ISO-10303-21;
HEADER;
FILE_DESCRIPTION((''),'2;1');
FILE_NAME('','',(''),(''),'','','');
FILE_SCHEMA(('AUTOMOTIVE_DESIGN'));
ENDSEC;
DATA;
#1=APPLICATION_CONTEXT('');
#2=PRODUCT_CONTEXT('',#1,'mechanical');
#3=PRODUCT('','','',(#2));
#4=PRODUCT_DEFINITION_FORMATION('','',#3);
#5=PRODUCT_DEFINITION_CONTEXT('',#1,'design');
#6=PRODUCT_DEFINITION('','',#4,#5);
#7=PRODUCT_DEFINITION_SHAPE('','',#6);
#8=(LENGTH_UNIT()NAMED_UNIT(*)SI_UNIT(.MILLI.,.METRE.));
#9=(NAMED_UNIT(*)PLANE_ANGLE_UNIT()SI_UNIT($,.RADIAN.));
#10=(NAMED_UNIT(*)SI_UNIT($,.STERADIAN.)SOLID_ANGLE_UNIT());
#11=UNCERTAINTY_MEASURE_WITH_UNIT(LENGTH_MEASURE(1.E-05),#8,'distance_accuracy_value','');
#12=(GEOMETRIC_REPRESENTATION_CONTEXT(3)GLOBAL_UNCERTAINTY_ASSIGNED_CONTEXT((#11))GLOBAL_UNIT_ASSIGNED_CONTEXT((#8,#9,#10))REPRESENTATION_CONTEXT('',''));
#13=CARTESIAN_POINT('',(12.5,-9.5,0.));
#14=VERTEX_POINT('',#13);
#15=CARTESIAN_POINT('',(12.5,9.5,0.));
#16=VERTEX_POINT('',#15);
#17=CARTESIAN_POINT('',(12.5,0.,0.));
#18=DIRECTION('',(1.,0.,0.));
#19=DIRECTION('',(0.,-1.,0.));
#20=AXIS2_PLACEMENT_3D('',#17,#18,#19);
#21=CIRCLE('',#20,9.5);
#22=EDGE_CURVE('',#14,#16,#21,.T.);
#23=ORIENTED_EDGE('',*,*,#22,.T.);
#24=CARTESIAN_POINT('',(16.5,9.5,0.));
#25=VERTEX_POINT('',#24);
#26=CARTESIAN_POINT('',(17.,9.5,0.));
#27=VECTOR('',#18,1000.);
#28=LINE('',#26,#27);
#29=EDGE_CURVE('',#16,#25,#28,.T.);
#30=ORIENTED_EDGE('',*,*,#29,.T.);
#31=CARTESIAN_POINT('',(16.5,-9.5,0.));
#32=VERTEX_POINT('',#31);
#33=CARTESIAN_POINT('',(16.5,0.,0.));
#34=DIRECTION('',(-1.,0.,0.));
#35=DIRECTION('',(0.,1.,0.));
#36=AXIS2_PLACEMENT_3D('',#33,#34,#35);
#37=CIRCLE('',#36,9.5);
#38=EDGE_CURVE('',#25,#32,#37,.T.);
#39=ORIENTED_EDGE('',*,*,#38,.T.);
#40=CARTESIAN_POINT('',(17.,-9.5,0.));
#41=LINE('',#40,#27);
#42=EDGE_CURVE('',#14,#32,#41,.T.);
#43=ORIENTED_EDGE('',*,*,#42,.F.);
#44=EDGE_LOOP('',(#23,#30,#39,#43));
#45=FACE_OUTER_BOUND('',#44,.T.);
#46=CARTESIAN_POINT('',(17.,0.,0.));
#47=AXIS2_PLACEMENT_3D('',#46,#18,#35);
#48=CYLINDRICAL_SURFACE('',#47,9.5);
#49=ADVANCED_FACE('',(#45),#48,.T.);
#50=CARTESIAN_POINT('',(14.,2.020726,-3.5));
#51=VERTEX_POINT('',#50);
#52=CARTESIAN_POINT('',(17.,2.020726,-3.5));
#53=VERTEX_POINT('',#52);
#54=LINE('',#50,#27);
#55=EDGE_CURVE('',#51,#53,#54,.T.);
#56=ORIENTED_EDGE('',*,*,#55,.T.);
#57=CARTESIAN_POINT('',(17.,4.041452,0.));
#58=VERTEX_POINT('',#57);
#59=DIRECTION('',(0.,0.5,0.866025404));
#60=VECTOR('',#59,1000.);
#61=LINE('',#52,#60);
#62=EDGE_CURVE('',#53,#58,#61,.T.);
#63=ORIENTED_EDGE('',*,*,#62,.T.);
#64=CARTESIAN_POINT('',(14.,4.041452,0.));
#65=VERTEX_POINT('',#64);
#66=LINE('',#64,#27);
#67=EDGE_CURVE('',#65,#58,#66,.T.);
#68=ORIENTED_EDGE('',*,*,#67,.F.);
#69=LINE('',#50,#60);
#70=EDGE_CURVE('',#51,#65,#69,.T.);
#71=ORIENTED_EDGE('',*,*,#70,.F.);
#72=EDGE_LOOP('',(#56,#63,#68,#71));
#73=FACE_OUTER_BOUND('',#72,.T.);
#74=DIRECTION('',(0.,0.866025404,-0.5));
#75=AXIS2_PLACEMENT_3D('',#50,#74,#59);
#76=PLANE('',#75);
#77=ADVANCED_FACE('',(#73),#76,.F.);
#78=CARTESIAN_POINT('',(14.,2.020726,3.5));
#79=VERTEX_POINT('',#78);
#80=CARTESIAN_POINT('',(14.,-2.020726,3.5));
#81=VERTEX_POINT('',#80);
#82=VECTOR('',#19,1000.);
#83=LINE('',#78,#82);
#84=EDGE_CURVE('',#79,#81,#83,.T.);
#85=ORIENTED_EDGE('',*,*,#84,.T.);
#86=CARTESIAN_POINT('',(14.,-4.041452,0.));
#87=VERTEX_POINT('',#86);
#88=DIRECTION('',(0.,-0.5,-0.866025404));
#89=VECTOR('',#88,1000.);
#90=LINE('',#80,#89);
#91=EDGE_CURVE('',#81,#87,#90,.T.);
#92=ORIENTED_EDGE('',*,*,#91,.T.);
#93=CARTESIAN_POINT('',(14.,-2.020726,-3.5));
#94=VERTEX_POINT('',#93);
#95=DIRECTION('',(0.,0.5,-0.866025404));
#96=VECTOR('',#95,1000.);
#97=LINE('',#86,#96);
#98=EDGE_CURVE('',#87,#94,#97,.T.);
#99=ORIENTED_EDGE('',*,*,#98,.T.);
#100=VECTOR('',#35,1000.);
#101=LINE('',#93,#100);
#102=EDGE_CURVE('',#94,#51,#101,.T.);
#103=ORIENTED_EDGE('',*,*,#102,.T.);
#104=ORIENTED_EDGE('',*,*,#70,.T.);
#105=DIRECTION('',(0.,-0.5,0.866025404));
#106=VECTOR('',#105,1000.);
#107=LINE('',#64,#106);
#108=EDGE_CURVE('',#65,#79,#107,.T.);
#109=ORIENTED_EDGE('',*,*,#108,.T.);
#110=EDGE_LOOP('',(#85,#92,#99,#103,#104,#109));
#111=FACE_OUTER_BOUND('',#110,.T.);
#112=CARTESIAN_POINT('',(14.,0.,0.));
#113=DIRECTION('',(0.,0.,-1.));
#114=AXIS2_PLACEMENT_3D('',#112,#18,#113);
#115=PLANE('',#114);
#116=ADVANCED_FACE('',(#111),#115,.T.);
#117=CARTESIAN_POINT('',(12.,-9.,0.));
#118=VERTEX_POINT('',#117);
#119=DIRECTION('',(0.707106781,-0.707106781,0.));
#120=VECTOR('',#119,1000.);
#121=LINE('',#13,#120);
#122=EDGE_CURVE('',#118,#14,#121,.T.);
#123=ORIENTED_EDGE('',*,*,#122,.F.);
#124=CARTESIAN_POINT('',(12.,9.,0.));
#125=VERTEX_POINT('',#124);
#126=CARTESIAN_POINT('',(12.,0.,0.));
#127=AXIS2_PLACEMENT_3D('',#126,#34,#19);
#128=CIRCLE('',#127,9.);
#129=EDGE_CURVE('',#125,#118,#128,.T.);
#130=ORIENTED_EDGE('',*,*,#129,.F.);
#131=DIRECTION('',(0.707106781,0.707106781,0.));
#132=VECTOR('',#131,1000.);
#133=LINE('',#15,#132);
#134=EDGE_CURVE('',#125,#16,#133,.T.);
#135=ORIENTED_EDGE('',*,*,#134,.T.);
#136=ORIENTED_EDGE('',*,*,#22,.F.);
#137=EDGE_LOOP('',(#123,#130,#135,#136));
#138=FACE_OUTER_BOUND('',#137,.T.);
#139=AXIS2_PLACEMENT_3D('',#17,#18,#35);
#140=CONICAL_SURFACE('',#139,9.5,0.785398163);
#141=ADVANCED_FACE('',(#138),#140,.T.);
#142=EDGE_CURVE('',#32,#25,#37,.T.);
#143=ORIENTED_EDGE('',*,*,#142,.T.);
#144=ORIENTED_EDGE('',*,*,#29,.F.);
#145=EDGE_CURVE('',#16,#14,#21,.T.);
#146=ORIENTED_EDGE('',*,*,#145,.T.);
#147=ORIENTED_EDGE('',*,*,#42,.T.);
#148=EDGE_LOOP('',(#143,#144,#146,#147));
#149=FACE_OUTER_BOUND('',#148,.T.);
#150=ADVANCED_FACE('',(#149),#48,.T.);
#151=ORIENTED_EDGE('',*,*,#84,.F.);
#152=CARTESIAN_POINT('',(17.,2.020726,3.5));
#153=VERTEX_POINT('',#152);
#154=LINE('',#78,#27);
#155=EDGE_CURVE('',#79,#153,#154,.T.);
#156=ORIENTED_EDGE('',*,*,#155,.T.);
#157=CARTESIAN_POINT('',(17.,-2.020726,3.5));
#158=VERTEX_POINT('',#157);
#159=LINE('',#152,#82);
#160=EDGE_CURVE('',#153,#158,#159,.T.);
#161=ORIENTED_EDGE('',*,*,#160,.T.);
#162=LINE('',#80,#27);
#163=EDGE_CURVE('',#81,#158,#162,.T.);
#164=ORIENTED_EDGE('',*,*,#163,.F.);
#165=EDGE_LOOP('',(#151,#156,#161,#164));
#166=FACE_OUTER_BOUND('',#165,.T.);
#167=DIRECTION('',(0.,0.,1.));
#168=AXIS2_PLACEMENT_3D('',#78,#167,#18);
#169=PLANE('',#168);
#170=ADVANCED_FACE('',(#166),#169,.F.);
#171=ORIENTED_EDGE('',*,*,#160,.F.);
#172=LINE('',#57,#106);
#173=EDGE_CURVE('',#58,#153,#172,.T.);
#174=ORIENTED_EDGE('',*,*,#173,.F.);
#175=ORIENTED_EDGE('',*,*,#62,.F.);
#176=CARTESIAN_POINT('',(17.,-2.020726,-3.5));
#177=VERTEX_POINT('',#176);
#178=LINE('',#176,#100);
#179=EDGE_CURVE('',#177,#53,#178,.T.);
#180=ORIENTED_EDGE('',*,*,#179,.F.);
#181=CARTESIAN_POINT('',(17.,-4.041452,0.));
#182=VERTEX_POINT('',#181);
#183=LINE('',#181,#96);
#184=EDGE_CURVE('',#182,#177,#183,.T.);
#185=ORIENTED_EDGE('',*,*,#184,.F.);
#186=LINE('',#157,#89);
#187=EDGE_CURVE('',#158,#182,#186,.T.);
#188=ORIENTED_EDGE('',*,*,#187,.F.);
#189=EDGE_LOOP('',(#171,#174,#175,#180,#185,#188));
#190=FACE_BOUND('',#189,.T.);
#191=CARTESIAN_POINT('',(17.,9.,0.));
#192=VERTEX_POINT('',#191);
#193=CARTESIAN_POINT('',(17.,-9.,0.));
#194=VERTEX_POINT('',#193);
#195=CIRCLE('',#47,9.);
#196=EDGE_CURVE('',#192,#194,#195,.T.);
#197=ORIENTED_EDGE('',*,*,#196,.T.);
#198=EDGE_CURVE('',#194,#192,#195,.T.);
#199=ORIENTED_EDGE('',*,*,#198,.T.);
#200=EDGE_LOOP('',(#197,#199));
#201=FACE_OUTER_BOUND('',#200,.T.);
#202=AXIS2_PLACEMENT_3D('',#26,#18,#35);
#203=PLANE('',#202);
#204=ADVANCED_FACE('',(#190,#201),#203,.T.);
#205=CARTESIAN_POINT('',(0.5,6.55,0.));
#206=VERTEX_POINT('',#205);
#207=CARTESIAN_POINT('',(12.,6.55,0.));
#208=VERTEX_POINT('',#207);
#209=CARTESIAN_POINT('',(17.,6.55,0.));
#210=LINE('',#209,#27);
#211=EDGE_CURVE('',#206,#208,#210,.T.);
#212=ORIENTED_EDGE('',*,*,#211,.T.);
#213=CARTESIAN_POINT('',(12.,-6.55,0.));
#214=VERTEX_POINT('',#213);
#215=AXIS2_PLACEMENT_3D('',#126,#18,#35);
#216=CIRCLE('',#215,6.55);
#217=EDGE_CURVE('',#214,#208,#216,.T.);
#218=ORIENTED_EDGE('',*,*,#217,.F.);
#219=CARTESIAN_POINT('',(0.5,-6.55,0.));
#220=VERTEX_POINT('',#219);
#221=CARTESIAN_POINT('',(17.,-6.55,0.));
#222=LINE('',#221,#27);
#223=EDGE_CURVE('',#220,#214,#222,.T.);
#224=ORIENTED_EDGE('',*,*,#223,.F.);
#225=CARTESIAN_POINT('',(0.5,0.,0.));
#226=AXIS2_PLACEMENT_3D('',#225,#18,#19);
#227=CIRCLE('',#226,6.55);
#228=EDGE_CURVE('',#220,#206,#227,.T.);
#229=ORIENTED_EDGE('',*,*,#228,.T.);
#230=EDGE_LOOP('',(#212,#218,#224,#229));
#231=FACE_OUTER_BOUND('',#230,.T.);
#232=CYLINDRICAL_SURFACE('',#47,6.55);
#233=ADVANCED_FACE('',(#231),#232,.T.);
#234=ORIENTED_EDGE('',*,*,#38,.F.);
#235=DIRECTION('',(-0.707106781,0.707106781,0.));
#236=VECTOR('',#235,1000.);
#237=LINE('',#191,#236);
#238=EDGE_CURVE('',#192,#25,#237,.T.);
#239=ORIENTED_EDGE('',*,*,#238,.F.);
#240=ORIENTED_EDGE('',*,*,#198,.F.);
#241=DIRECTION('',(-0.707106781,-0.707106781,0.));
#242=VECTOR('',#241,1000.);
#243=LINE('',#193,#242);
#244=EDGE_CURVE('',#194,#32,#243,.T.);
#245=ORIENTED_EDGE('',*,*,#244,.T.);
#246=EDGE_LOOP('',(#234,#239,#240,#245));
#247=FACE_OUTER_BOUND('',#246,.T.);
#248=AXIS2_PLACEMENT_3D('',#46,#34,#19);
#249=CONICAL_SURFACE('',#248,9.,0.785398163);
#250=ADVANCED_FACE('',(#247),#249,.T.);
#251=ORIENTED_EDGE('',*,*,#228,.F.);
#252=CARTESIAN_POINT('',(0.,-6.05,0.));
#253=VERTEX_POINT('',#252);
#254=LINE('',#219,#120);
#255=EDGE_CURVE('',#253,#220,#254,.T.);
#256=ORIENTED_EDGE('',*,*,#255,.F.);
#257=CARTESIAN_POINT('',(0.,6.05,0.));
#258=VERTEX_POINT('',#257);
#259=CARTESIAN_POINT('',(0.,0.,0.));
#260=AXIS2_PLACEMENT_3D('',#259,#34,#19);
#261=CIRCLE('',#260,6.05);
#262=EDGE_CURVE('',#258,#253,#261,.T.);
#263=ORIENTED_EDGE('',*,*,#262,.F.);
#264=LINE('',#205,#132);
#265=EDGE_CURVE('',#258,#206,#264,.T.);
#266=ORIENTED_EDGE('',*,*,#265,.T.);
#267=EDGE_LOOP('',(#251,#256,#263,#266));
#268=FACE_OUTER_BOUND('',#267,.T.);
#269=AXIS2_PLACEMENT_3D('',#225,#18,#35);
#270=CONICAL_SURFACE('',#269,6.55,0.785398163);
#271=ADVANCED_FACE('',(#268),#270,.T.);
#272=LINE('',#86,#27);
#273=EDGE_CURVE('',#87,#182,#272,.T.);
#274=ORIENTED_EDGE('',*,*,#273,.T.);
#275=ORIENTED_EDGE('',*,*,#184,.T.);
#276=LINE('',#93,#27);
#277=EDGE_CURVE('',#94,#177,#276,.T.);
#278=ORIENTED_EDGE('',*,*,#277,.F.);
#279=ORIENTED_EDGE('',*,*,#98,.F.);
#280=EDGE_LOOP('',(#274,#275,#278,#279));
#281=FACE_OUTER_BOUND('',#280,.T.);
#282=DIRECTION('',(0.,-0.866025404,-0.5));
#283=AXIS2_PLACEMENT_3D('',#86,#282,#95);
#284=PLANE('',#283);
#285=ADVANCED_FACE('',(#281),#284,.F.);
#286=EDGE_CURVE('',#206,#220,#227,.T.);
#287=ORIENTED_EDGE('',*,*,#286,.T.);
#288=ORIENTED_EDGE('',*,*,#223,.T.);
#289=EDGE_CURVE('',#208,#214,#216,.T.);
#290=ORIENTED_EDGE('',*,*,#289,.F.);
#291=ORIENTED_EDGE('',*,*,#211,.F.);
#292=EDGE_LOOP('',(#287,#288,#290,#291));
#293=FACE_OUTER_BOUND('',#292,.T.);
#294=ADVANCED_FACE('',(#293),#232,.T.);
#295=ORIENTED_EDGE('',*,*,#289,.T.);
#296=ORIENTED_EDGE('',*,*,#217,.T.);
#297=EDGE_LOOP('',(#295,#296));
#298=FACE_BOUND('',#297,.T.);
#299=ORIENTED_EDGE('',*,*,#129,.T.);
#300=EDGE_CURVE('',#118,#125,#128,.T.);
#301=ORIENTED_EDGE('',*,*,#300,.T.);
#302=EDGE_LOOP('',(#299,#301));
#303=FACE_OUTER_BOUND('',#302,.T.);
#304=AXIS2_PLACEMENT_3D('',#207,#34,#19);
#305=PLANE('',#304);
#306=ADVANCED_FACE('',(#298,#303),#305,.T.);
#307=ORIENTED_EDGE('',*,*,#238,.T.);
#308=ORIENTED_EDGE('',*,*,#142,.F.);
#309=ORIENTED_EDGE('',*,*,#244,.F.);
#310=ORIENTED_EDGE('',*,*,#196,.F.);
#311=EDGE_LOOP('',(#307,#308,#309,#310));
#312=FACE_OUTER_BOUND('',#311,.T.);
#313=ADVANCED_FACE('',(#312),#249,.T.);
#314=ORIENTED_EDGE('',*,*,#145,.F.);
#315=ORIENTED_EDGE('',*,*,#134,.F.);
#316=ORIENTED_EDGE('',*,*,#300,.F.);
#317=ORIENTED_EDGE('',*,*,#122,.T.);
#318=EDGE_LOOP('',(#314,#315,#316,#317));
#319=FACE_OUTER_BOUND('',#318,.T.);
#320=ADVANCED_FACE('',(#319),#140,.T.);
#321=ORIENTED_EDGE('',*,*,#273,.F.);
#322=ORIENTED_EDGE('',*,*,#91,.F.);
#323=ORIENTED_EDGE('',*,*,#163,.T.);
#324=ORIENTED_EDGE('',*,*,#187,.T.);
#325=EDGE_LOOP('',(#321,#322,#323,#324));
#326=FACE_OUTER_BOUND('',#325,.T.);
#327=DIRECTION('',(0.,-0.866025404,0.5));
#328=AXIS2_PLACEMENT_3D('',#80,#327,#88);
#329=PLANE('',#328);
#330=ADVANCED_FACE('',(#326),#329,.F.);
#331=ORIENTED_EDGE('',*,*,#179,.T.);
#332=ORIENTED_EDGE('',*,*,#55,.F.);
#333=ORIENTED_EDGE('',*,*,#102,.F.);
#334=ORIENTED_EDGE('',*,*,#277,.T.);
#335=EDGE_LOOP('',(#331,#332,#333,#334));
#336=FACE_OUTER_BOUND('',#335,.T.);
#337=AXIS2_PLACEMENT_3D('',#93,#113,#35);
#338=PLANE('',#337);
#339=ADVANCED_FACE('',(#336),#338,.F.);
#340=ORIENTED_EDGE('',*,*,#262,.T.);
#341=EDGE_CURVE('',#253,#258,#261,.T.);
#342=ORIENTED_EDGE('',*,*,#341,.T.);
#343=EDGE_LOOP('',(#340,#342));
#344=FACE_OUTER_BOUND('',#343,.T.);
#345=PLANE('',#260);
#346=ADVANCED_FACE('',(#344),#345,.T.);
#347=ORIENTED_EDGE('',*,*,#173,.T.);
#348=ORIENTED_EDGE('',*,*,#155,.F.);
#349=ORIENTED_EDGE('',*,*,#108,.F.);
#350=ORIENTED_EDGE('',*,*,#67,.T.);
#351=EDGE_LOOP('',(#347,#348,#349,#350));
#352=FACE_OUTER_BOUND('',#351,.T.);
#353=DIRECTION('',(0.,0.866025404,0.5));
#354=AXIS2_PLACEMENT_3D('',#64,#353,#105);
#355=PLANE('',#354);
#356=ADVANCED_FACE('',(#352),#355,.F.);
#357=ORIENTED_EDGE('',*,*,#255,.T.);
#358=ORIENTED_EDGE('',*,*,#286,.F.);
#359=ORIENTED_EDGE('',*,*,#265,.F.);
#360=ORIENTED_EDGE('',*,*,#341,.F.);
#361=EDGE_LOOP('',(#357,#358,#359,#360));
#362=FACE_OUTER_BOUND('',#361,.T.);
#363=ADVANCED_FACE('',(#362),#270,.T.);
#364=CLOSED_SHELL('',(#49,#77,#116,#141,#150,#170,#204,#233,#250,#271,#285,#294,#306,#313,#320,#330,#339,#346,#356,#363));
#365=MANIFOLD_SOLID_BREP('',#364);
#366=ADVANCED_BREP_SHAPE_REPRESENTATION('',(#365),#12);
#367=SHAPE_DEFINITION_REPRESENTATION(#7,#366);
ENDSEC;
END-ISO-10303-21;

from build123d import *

# Parameters (mm, degrees)
CUT_EXTRUDE1_DEPTH = 3
CHAMFER1_SIZE      = 0.5


with BuildPart() as part:
    # Sketch1 → Revolve1 (revolve)
    with BuildSketch(Plane.XY):
        Polygon((0, 0), (0, 6.55), (12, 6.55), (12, 9.5), (17, 9.5), (17, 0), align=None)
    revolve(axis=Axis((17, 0, 0), (-1, 0, 0)))

    # Sketch2 → Cut-Extrude1 (cut)
    with BuildSketch(Plane(origin=(17, 0, 0), x_dir=(0, 0, -1), z_dir=(1, 0, 0))):
        Polygon((0, 4.041451884), (-3.5, 2.020725942), (-3.5, -2.020725942), (0, -4.041451884), (3.5, -2.020725942), (3.5, 2.020725942), align=None)
    extrude(amount=-CUT_EXTRUDE1_DEPTH, mode=Mode.SUBTRACT)

    # Chamfer1
    chamfer1_edges = [part.edges().sort_by_distance(p)[0] for p in [
        (17, -9.5, 0),
        (12, -9.5, 0),
        (0, -6.55, 0),
    ]]
    chamfer(chamfer1_edges, length=CHAMFER1_SIZE)


solid = part.part
